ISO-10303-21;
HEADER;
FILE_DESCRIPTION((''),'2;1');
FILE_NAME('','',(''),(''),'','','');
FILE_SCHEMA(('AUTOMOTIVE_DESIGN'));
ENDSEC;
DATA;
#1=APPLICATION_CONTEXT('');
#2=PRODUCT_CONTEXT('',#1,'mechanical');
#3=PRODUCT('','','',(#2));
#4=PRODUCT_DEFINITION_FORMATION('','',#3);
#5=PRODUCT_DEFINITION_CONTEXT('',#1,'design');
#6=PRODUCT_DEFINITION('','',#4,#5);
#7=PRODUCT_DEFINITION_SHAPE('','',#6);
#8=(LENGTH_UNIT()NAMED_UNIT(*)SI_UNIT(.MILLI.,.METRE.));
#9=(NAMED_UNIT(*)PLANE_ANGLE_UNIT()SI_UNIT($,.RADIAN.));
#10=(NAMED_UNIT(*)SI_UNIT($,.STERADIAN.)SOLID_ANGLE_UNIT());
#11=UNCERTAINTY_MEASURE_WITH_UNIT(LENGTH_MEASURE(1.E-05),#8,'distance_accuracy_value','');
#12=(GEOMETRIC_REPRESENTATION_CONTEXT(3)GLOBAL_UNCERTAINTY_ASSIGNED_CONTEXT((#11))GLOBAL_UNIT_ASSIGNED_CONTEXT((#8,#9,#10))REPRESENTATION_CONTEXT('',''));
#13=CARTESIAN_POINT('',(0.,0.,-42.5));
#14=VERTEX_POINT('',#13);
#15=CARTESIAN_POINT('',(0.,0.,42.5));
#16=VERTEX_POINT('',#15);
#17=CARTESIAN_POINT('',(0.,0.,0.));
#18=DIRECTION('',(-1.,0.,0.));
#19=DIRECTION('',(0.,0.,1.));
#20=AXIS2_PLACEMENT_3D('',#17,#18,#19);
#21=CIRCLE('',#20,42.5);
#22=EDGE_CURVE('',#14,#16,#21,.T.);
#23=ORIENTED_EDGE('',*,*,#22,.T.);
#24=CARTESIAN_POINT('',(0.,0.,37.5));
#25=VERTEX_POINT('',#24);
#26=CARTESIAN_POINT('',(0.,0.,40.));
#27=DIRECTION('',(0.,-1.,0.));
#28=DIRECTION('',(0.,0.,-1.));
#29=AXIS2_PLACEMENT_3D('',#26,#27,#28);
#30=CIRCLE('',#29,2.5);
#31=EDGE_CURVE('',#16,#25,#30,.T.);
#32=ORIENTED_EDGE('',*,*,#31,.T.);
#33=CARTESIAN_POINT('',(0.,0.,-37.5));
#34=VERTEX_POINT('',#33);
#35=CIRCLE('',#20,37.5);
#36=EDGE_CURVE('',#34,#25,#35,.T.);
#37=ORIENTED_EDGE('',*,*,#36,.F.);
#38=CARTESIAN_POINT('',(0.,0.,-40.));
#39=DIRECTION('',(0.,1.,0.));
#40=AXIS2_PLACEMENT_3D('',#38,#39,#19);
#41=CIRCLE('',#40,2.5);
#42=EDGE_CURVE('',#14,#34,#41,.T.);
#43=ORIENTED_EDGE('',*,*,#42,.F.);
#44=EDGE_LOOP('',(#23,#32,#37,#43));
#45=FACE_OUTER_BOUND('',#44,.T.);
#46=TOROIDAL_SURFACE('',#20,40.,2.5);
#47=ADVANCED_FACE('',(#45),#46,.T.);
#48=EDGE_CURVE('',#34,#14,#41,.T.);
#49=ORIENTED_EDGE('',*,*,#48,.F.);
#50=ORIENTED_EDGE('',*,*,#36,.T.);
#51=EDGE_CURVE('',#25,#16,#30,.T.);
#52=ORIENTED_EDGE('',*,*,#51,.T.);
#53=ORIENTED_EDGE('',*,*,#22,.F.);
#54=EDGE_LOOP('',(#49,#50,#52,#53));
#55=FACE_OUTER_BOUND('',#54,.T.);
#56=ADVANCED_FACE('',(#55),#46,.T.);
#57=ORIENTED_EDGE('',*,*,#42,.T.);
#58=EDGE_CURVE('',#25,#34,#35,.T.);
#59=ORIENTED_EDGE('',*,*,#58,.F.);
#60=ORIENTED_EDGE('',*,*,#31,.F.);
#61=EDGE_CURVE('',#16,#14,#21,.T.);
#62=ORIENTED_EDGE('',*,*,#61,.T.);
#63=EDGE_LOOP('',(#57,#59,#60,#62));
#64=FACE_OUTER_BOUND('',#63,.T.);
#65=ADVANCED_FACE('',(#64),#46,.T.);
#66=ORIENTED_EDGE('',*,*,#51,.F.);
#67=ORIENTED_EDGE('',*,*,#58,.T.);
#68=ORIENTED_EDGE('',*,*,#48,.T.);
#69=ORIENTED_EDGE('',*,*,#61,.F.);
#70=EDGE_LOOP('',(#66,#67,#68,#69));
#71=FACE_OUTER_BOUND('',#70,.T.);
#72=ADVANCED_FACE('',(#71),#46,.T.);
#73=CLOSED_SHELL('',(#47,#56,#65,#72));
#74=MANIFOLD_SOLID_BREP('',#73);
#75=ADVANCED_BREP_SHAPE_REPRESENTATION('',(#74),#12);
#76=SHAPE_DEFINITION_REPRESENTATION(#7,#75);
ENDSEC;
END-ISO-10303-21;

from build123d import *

# Parameters (mm, degrees)
SKETCH_1_R = 2.5


with BuildPart() as part:
    # 草图1 → 旋转1 (revolve)
    with BuildSketch(Plane.XY, mode=Mode.PRIVATE) as revolve_1_sk:
        with Locations((0, 40)):
            Circle(SKETCH_1_R)
    revolve(revolve_1_sk.sketch.rotate(Axis((-21.92893401, 0, 0), (1, 0, 0)), 90), axis=Axis((-21.92893401, 0, 0), (1, 0, 0)))


solid = part.part
